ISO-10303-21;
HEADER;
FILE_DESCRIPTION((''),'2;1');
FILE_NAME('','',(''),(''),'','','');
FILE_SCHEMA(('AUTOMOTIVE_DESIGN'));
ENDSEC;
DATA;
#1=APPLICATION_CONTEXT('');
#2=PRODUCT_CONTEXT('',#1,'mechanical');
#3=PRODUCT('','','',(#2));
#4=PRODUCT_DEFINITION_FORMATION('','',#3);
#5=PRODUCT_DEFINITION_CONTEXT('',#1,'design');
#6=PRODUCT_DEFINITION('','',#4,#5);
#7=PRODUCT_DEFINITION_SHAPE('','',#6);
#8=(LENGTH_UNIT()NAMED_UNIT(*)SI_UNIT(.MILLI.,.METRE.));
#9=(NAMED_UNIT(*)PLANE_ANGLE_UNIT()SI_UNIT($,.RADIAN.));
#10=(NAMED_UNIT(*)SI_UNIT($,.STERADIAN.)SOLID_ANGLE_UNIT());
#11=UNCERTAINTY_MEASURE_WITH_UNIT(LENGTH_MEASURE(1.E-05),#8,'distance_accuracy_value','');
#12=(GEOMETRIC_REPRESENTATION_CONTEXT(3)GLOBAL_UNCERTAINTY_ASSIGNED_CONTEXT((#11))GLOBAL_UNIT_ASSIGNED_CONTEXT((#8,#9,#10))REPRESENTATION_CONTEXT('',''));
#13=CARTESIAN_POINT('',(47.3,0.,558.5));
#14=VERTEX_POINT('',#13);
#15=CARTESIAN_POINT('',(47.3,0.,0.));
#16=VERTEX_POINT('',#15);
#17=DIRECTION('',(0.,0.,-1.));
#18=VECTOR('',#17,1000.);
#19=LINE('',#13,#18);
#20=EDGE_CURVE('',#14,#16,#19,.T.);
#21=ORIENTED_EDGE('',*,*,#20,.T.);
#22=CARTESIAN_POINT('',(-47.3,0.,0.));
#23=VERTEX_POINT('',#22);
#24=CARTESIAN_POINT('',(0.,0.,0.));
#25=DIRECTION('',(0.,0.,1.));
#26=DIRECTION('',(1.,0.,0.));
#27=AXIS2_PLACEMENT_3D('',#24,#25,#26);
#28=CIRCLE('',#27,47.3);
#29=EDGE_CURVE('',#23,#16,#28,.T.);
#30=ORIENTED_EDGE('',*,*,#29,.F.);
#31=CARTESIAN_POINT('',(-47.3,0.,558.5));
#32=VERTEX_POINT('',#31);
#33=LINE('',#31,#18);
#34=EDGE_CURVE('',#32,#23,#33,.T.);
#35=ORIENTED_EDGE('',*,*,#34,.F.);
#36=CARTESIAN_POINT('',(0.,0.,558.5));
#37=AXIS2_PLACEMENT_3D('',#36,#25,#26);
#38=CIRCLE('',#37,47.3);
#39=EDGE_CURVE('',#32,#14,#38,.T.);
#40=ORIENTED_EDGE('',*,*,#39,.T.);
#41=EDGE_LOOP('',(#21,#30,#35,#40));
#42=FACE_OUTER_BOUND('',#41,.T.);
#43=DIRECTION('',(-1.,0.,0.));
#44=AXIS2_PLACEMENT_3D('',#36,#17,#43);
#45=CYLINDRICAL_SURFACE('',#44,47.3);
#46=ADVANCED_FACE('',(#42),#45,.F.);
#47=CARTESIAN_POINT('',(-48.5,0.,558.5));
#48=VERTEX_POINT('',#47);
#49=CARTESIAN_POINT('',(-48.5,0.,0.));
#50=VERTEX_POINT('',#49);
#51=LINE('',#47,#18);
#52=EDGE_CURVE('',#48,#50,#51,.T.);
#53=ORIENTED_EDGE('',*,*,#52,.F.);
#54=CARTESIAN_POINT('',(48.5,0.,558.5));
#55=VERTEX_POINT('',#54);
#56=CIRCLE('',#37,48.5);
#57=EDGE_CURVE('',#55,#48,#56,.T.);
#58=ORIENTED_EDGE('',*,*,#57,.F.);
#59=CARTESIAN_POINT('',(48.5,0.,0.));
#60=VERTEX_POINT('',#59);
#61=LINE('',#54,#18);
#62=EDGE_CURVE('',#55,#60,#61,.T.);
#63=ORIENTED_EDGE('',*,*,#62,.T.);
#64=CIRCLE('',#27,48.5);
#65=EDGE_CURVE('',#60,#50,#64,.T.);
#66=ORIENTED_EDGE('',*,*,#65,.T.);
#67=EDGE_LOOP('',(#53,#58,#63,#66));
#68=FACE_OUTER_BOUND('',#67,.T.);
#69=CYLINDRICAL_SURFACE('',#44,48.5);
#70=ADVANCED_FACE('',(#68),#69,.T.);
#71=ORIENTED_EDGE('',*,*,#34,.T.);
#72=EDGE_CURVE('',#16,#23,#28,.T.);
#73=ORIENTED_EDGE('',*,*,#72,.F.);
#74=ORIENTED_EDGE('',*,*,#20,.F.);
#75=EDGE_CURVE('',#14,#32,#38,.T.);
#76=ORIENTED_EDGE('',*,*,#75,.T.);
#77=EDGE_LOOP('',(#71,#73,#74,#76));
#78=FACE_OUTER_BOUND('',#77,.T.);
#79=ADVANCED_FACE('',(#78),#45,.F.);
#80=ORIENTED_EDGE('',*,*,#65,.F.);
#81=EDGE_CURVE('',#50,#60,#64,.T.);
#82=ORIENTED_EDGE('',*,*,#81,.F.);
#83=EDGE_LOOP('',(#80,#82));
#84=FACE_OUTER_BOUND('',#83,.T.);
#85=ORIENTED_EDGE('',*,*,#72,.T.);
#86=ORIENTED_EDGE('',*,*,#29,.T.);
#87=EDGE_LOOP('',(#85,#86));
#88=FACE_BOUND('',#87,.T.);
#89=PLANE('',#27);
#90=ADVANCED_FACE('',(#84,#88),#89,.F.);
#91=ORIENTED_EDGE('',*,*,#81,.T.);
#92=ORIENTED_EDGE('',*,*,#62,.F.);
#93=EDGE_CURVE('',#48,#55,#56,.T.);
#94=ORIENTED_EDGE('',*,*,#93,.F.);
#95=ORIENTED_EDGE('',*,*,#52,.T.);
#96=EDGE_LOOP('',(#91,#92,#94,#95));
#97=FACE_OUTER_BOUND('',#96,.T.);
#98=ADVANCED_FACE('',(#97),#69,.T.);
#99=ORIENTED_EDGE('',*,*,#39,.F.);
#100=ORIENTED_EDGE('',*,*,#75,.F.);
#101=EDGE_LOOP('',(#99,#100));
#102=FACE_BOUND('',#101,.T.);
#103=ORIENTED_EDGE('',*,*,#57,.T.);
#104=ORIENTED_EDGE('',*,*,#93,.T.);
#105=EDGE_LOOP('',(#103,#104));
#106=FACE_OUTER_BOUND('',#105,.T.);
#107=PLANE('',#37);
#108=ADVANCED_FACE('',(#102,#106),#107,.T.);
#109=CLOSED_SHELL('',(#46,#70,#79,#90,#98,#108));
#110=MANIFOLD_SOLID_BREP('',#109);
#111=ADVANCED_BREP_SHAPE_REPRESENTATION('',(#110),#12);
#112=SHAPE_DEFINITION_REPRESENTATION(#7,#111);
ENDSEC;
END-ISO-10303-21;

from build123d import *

# Parameters (mm, degrees)
SKETCH_1_R      = 48.5
SKETCH_1_R_2    = 47.3
EXTRUDE_1_DEPTH = 558.5


with BuildPart() as part:
    # 草图1 → 凸台-拉伸1 (new body)
    with BuildSketch(Plane.XY):
        Circle(SKETCH_1_R)
        Circle(SKETCH_1_R_2, mode=Mode.SUBTRACT)
    extrude(amount=EXTRUDE_1_DEPTH)


solid = part.part
